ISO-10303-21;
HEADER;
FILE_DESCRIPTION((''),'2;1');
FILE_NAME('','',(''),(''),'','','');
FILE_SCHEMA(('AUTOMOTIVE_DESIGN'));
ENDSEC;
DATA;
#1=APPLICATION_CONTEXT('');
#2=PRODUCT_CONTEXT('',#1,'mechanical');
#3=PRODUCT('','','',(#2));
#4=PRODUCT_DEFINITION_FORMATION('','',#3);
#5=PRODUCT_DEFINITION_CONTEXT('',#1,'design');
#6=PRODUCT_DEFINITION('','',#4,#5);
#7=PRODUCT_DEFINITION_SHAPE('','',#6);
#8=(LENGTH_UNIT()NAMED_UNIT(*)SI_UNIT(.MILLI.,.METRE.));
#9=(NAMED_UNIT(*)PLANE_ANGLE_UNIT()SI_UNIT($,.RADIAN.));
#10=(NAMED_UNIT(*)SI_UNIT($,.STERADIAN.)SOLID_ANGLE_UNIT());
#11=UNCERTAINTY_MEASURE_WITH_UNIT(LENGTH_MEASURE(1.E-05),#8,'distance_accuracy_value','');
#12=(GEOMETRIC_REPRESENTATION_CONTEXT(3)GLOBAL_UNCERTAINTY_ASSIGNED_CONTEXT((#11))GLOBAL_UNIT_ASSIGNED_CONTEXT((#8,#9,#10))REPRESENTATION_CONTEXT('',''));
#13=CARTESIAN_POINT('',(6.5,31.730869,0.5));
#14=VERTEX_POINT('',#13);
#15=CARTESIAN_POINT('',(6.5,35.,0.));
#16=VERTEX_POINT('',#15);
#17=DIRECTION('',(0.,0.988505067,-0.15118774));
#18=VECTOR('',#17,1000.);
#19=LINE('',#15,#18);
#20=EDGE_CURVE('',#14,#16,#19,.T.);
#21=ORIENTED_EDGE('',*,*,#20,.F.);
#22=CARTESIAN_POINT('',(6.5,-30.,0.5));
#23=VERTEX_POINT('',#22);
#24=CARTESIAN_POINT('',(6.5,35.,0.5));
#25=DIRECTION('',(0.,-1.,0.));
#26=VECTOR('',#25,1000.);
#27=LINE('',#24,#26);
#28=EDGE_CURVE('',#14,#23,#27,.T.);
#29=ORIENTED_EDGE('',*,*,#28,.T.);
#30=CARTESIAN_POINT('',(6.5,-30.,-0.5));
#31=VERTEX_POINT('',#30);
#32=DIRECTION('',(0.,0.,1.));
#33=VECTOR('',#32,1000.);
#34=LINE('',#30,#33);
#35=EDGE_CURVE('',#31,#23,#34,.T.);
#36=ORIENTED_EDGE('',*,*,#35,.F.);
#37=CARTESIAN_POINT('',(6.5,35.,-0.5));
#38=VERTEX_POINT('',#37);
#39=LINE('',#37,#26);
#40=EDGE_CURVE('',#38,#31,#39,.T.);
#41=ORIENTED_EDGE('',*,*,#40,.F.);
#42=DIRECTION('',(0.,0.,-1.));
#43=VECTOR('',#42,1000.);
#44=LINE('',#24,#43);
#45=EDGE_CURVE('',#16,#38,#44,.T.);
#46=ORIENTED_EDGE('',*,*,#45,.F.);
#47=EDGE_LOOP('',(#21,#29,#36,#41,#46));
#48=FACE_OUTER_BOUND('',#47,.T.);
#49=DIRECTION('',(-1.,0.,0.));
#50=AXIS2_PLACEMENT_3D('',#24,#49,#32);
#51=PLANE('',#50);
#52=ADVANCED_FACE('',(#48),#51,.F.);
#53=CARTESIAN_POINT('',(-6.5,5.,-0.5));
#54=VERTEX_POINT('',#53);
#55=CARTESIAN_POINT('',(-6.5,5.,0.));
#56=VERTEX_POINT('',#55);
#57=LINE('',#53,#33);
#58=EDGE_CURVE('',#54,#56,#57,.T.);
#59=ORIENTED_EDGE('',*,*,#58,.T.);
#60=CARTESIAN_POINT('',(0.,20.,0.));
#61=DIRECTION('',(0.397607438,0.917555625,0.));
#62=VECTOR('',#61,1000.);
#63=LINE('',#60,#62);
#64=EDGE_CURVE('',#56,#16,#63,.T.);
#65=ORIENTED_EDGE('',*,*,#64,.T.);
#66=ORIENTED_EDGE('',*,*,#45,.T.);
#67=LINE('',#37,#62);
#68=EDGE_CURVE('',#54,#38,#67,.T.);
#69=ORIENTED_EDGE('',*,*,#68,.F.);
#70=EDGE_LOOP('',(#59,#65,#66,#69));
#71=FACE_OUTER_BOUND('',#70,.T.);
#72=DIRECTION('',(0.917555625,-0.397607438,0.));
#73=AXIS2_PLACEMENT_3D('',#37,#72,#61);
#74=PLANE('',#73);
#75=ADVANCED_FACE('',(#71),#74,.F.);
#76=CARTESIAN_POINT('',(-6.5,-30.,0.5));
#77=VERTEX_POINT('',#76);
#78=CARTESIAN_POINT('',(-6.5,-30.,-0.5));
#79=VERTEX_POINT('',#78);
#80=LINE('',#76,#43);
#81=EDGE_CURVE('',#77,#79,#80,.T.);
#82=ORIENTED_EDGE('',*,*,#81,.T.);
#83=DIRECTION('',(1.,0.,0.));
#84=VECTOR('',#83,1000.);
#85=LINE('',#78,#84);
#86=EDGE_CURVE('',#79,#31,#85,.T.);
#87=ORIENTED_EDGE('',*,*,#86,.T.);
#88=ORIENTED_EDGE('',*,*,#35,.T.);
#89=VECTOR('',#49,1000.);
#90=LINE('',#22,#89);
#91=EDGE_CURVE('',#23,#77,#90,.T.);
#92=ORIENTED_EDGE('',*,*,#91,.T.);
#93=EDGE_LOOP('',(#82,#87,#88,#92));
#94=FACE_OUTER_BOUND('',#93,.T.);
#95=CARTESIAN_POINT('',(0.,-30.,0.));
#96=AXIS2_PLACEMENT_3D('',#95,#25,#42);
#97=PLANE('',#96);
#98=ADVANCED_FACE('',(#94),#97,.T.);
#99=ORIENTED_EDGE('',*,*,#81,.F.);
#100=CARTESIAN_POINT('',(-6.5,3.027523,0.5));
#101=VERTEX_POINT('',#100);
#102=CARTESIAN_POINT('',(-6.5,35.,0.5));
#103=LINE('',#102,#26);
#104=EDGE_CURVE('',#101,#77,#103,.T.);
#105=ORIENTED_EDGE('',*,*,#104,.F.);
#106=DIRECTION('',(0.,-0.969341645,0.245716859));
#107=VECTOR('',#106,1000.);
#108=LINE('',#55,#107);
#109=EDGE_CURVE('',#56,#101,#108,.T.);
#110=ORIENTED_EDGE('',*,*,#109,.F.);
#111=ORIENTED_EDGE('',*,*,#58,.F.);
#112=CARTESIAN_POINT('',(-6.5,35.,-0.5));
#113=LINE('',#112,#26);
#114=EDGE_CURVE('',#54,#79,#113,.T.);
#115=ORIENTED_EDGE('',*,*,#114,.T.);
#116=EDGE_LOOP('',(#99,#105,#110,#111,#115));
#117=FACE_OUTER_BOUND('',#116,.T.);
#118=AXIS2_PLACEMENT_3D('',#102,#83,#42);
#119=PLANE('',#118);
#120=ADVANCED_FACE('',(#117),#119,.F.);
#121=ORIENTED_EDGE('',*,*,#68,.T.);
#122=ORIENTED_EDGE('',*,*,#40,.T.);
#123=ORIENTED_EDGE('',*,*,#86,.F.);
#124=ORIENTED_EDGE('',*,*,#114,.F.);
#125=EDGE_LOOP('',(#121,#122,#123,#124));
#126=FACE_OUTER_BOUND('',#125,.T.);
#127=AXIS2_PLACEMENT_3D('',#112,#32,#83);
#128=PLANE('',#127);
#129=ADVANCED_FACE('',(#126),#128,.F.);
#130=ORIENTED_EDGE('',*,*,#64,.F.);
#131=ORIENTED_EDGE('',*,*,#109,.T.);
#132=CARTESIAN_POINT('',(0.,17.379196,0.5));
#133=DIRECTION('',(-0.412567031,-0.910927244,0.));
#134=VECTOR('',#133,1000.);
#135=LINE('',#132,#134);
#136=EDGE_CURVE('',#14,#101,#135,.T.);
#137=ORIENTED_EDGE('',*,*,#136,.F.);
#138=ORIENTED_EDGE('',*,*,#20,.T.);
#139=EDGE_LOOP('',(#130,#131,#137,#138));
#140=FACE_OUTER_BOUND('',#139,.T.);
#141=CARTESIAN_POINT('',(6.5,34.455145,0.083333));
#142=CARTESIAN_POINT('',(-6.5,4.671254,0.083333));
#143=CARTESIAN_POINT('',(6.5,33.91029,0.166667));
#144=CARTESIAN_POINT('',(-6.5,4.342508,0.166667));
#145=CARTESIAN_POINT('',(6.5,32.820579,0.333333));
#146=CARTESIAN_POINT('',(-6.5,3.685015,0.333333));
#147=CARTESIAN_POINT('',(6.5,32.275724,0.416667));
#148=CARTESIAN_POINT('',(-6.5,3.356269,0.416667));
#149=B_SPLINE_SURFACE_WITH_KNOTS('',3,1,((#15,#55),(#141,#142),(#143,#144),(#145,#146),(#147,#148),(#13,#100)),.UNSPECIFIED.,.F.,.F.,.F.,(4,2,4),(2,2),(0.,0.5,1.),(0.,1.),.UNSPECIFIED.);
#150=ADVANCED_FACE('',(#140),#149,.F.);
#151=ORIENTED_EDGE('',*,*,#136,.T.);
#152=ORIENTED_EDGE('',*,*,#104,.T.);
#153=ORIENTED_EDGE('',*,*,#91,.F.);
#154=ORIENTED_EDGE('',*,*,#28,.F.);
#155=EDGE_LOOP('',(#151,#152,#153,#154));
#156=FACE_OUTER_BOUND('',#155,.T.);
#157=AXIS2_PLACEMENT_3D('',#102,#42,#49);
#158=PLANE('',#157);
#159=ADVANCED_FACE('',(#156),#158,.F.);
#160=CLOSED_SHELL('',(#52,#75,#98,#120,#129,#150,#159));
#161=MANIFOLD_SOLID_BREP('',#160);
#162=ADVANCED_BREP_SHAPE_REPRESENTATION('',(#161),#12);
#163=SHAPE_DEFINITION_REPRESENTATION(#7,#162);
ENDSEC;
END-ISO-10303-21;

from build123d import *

# Parameters (mm, degrees)
SKETCH1_W           = 13
SKETCH1_H           = 1
BOSS_EXTRUDE1_DEPTH = 35
CUT_EXTRUDE2_DEPTH  = 36.612497806
SKETCH8_W           = 13
SKETCH8_H           = 1
BOSS_EXTRUDE2_DEPTH = 30


with BuildPart() as part:
    # Sketch1 → Boss-Extrude1 (new body)
    with BuildSketch(Plane(origin=(0, 0, 0), x_dir=(1, 0, 0), z_dir=(0, 1, 0))):
        Rectangle(SKETCH1_W, SKETCH1_H)
    extrude(amount=BOSS_EXTRUDE1_DEPTH)

    # Sketch3 → Cut-Extrude2 (cut, through all)
    with BuildSketch(Plane.XY.offset(0.5)):
        Polygon((6.5, 35), (-6.5, 5), (-6.5, 35), align=None)
    extrude(amount=-CUT_EXTRUDE2_DEPTH, mode=Mode.SUBTRACT)

    # Sketch7 → Cut-Loft2 section 0
    with BuildSketch(Plane(origin=(6.5, 0, 0), x_dir=(0, 0, -1), z_dir=(1, 0, 0))):
        with BuildLine():
            Line((0, 35), (-0.5, 31.730868962))
            Line((-0.5, 31.730868962), (-0.5, 35))
            Line((-0.5, 35), (0, 35))
        make_face()
    # Sketch6 → Cut-Loft2 section 1
    with BuildSketch(Plane.ZY.offset(6.5)):
        with BuildLine():
            Line((0, 5), (0.5, 3.027523124))
            Line((0.5, 3.027523124), (0.5, 5))
            Line((0.5, 5), (0, 5))
        make_face()
    loft(mode=Mode.SUBTRACT)

    # Sketch8 → Boss-Extrude2 (add)
    with BuildSketch(Plane.XZ):
        Rectangle(SKETCH8_W, SKETCH8_H)
    extrude(amount=BOSS_EXTRUDE2_DEPTH)


solid = part.part
